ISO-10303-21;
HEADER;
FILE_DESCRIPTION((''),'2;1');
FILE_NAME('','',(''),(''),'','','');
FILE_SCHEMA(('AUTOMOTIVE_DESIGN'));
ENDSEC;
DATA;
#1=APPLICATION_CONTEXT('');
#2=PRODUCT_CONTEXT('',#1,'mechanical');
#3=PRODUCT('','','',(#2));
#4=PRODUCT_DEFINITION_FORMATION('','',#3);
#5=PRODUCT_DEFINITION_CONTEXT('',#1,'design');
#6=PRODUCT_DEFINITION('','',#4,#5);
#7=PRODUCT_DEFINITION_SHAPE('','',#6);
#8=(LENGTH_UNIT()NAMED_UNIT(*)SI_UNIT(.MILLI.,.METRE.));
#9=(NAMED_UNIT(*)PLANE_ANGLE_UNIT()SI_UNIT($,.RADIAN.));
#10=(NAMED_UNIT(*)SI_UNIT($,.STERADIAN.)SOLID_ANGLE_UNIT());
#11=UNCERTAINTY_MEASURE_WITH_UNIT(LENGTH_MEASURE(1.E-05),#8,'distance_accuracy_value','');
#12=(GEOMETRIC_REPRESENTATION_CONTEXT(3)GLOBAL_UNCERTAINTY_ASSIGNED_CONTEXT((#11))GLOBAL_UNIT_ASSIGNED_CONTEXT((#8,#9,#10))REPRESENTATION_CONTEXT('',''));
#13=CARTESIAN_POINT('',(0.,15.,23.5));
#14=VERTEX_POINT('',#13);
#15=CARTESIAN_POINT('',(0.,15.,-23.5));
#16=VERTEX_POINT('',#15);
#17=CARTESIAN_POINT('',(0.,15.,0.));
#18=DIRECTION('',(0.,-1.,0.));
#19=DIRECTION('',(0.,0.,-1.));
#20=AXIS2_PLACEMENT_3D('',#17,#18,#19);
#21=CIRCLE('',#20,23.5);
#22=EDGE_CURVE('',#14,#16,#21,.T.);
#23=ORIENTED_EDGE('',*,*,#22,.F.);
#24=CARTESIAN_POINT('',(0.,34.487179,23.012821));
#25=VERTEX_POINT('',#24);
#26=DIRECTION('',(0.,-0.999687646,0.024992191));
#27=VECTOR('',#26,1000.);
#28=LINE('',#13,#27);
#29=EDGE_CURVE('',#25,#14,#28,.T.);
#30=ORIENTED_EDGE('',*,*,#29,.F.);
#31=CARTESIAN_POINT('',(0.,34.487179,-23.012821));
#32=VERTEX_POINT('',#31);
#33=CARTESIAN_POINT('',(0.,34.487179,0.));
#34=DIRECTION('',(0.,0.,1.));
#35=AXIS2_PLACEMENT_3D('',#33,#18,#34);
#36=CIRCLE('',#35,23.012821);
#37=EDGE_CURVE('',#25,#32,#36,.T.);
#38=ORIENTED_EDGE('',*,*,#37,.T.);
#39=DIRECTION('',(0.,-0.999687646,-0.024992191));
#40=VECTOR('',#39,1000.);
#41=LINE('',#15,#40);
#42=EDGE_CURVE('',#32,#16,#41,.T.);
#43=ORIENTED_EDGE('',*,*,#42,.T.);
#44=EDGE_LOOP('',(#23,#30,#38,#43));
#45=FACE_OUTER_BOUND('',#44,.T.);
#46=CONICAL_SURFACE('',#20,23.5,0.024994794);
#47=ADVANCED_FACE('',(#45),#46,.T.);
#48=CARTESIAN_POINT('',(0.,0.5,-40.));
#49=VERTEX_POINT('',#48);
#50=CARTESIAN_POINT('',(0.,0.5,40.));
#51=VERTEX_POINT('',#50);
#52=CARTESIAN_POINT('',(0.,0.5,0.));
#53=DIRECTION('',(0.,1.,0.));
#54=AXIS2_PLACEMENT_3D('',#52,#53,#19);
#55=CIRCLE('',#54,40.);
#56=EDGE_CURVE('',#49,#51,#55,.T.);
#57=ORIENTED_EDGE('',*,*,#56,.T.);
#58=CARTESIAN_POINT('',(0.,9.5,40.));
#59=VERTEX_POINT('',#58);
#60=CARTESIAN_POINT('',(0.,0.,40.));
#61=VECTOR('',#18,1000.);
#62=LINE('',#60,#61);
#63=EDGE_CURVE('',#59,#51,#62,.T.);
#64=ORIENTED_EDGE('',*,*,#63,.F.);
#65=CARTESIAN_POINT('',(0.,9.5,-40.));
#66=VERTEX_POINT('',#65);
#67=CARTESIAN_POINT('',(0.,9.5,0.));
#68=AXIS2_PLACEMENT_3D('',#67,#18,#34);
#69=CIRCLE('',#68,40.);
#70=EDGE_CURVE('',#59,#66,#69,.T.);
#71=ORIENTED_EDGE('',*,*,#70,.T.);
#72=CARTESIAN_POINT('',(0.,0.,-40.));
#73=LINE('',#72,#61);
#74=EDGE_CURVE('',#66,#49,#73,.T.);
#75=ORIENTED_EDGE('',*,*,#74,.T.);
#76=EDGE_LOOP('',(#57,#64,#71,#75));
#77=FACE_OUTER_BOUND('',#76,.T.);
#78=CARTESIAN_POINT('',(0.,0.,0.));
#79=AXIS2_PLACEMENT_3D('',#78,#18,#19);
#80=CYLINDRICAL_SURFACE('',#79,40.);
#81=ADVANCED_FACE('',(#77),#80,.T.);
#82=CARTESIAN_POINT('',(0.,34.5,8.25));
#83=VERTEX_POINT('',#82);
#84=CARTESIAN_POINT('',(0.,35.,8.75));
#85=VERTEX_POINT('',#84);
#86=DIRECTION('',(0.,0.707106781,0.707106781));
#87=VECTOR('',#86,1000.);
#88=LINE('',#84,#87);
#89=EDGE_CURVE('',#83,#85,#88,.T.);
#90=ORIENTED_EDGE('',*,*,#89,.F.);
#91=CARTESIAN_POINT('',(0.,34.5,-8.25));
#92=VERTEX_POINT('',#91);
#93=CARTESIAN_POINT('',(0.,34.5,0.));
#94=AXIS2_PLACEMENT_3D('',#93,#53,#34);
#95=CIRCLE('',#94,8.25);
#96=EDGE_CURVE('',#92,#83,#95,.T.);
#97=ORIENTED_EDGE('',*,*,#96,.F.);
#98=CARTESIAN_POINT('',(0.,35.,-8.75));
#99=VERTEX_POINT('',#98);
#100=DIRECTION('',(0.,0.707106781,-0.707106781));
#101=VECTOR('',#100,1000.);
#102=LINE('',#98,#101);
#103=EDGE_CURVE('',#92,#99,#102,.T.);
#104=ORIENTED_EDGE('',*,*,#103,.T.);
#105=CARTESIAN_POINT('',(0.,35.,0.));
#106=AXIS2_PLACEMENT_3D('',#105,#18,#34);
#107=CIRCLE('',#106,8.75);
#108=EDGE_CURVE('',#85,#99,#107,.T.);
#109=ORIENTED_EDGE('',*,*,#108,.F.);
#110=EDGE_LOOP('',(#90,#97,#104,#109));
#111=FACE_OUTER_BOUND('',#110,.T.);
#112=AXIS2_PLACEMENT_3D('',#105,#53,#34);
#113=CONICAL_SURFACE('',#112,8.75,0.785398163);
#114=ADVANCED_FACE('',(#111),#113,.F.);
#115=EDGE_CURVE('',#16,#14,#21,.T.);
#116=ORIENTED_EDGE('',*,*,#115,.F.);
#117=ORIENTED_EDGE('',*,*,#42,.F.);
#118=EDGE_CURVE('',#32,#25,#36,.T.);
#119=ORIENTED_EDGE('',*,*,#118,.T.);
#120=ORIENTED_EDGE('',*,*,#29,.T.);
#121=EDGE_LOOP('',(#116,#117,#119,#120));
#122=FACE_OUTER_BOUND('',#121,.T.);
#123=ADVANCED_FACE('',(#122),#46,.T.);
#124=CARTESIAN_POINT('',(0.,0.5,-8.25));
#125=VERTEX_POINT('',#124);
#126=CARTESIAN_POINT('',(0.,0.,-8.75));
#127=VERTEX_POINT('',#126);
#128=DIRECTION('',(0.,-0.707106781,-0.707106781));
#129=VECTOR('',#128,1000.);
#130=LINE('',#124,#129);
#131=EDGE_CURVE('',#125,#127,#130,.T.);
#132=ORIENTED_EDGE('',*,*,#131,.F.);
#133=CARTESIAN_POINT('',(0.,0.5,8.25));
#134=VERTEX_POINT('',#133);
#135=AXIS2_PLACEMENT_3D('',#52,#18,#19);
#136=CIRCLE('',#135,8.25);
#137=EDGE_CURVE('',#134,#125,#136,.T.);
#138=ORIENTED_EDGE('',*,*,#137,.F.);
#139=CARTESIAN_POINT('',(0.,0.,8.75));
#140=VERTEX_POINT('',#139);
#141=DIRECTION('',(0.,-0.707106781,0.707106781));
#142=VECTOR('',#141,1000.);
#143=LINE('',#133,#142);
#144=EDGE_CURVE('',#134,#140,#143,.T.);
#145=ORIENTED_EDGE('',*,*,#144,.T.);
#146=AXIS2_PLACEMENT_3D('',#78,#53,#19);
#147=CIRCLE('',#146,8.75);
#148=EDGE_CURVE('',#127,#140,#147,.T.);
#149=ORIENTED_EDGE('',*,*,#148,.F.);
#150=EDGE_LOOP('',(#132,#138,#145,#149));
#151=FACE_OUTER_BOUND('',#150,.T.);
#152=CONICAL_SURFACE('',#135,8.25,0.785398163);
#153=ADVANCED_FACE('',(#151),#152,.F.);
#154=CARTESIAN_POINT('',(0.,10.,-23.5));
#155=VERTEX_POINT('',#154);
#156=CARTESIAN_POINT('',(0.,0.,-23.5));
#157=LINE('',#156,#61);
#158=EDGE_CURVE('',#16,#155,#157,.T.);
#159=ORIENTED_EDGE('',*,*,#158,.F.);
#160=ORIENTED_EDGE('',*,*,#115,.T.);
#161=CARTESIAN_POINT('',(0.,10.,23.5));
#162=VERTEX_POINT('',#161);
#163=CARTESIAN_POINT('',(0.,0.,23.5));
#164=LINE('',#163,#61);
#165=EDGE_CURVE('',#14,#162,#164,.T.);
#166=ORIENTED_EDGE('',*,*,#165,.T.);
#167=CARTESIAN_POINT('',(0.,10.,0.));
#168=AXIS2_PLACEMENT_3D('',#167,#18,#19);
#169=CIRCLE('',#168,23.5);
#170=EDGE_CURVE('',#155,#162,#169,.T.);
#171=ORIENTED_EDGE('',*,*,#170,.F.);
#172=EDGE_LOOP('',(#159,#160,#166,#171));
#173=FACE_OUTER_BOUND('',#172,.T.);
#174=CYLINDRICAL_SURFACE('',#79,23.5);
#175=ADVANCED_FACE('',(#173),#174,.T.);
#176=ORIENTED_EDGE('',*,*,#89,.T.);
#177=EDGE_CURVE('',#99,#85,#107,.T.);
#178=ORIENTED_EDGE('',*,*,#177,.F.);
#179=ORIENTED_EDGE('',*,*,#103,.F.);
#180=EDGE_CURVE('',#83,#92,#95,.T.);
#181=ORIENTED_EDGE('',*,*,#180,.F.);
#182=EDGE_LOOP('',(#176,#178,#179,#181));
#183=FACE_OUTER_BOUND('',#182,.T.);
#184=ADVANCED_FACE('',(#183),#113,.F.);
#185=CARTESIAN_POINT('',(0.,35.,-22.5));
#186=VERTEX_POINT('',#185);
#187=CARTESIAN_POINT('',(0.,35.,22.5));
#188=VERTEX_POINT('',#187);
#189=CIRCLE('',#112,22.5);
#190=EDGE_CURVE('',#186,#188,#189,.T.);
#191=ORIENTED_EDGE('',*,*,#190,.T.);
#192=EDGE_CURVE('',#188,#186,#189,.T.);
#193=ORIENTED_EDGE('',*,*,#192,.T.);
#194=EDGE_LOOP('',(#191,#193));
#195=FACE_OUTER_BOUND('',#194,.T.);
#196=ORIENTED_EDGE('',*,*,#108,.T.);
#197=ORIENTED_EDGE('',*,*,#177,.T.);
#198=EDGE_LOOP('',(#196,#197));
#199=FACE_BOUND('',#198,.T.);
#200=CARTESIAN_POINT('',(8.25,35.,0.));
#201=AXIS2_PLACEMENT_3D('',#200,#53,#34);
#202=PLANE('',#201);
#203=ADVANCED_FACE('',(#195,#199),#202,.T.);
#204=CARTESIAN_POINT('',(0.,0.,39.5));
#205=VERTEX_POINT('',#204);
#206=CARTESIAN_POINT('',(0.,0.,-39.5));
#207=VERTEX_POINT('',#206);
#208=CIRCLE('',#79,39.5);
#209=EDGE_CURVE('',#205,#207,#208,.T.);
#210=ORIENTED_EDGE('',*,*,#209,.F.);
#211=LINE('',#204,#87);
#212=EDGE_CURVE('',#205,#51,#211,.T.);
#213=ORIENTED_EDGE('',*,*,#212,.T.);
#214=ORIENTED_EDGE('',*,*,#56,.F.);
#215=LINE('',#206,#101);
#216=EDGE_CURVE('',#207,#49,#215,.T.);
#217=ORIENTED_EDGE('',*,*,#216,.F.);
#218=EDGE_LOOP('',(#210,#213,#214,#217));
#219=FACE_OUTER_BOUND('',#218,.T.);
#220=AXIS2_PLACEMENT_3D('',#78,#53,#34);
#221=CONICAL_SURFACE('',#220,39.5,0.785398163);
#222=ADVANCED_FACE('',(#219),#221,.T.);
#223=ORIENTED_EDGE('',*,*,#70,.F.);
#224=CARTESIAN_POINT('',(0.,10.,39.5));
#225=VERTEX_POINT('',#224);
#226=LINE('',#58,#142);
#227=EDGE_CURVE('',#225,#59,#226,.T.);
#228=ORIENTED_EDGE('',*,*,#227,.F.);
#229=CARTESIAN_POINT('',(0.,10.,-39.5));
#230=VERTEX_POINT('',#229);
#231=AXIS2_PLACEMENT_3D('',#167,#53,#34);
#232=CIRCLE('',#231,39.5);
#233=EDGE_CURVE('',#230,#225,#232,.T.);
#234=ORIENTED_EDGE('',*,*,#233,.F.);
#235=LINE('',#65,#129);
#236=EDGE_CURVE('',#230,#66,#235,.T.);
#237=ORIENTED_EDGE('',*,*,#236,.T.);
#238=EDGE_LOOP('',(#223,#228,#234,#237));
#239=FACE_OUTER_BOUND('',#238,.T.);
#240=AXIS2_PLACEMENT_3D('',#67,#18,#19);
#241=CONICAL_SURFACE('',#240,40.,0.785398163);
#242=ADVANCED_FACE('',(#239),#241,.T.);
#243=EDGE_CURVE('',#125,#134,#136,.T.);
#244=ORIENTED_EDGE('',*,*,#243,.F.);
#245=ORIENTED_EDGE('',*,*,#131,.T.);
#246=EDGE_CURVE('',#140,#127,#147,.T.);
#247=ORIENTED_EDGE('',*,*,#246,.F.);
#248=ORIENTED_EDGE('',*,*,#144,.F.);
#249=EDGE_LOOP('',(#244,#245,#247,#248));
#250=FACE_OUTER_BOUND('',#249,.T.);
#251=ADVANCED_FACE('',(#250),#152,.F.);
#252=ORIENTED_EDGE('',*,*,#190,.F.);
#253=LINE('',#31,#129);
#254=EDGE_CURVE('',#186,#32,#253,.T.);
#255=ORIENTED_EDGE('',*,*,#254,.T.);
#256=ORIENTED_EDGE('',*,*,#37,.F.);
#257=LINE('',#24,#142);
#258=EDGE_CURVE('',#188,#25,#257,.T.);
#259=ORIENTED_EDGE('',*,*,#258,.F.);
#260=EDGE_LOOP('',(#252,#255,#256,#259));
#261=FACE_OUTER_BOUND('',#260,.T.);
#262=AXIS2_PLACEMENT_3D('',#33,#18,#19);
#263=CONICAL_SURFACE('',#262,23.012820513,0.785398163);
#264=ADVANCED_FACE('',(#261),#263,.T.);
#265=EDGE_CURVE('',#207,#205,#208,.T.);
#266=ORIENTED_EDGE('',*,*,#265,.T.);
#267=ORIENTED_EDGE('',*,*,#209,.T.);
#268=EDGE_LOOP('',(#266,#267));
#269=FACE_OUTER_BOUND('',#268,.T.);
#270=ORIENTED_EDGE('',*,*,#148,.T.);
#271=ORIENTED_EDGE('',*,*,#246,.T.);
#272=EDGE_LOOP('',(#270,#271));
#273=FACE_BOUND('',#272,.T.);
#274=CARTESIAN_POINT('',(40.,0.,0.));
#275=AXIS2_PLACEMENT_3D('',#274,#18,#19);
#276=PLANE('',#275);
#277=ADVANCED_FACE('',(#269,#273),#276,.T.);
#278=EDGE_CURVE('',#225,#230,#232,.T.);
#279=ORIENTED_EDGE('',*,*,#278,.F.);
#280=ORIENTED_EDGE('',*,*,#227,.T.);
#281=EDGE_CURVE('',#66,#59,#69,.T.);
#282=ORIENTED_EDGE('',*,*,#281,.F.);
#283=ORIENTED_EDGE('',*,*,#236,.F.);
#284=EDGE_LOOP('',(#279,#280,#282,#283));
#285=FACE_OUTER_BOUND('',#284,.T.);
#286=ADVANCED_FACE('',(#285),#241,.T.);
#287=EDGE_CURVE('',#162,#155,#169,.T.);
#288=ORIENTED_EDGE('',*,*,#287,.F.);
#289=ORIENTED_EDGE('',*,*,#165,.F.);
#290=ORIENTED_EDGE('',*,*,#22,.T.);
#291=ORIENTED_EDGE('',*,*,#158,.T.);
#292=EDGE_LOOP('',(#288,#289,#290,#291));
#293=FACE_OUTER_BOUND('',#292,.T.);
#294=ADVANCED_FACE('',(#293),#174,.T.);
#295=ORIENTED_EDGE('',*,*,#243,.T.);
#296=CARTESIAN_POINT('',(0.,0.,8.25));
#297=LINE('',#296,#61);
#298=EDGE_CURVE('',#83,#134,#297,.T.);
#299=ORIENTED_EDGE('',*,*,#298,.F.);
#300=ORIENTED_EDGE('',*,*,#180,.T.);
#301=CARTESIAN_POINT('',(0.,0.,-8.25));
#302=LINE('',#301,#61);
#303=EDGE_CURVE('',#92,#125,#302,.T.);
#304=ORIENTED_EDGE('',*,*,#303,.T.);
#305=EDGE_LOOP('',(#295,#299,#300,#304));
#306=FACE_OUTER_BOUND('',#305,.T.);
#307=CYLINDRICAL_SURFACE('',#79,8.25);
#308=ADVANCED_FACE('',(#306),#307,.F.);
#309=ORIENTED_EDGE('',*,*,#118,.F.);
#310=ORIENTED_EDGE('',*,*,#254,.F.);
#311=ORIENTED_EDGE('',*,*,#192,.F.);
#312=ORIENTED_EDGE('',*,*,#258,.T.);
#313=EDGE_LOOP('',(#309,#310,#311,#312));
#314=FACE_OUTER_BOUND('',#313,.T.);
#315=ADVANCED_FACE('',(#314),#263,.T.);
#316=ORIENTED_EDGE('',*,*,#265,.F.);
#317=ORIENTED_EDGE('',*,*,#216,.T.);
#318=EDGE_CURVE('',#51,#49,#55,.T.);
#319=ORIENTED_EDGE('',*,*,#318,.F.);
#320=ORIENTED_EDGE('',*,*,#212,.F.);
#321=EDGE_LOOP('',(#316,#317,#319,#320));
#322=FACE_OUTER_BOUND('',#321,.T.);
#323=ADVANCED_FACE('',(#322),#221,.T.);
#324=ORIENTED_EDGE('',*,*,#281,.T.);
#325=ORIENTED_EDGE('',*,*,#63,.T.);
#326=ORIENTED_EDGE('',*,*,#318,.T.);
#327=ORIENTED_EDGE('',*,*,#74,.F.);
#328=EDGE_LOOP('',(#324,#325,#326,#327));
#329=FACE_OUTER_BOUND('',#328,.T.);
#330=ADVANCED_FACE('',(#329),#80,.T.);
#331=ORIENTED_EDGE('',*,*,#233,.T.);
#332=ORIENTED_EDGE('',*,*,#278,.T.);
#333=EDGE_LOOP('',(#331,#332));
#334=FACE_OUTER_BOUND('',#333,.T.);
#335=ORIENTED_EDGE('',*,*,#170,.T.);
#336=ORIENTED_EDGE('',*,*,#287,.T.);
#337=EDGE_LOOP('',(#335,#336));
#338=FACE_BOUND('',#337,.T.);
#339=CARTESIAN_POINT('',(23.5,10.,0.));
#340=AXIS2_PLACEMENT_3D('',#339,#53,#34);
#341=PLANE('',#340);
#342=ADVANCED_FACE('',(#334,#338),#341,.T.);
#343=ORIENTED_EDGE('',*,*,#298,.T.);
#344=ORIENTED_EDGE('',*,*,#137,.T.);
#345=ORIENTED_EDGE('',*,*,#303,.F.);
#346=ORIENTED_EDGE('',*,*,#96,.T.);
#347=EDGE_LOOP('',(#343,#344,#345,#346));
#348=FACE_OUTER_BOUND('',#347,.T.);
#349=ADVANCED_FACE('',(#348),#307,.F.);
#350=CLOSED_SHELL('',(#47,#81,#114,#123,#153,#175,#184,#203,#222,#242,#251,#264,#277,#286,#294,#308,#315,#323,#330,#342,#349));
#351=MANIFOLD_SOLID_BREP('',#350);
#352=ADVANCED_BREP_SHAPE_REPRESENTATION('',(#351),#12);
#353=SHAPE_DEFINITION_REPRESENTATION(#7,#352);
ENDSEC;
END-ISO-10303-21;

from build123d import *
from OCP.BRepFilletAPI import BRepFilletAPI_MakeChamfer

# Parameters (mm, degrees)
CHAMFER1_SIZE  = 0.5
CHAMFER1_SIZE2 = 0.512980744


with BuildPart() as part:
    # Sketch1 → Revolve1 (revolve)
    with BuildSketch(Plane.XY, mode=Mode.PRIVATE) as revolve1_sk:
        Polygon((8.25, 35), (23, 35), (23.5, 15), (23.5, 10), (40, 10), (40, 0), (8.25, 0), align=None)
    revolve(revolve1_sk.sketch.rotate(Axis((0, 0, 0), (0, 1, 0)), 90), axis=Axis((0, 0, 0), (0, 1, 0)))

    # Chamfer1: one chamfer whose edges measure the first distance from different faces: ONE call of the kernel's chamfer builder (chamfer() names one face for all edges)
    chamfer1_edges_1 = [part.edges().sort_by_distance(p)[0] for p in [
        (0, 10, 40),
        (0, 0, 40),
        (0, 0, 8.25),
        (0, 35, 8.25),
    ]]
    chamfer1_edges_2 = [part.edges().sort_by_distance(p)[0] for p in [
        (0, 35, 23),
    ]]
    chamfer1_side_2 = [part.faces().sort_by_distance(p)[0] for p in [
        (0, 35, 8.900538239),
    ]]
    chamfer1 = BRepFilletAPI_MakeChamfer(part.part.solid().wrapped)
    for e in chamfer1_edges_1:
        chamfer1.Add(CHAMFER1_SIZE, e.wrapped)
    for e in chamfer1_edges_2:
        chamfer1.Add(CHAMFER1_SIZE, CHAMFER1_SIZE2, e.wrapped, chamfer1_side_2[0].wrapped)  # the first distance lies on this face
    add(Compound.cast(chamfer1.Shape()), mode=Mode.REPLACE)


solid = part.part
